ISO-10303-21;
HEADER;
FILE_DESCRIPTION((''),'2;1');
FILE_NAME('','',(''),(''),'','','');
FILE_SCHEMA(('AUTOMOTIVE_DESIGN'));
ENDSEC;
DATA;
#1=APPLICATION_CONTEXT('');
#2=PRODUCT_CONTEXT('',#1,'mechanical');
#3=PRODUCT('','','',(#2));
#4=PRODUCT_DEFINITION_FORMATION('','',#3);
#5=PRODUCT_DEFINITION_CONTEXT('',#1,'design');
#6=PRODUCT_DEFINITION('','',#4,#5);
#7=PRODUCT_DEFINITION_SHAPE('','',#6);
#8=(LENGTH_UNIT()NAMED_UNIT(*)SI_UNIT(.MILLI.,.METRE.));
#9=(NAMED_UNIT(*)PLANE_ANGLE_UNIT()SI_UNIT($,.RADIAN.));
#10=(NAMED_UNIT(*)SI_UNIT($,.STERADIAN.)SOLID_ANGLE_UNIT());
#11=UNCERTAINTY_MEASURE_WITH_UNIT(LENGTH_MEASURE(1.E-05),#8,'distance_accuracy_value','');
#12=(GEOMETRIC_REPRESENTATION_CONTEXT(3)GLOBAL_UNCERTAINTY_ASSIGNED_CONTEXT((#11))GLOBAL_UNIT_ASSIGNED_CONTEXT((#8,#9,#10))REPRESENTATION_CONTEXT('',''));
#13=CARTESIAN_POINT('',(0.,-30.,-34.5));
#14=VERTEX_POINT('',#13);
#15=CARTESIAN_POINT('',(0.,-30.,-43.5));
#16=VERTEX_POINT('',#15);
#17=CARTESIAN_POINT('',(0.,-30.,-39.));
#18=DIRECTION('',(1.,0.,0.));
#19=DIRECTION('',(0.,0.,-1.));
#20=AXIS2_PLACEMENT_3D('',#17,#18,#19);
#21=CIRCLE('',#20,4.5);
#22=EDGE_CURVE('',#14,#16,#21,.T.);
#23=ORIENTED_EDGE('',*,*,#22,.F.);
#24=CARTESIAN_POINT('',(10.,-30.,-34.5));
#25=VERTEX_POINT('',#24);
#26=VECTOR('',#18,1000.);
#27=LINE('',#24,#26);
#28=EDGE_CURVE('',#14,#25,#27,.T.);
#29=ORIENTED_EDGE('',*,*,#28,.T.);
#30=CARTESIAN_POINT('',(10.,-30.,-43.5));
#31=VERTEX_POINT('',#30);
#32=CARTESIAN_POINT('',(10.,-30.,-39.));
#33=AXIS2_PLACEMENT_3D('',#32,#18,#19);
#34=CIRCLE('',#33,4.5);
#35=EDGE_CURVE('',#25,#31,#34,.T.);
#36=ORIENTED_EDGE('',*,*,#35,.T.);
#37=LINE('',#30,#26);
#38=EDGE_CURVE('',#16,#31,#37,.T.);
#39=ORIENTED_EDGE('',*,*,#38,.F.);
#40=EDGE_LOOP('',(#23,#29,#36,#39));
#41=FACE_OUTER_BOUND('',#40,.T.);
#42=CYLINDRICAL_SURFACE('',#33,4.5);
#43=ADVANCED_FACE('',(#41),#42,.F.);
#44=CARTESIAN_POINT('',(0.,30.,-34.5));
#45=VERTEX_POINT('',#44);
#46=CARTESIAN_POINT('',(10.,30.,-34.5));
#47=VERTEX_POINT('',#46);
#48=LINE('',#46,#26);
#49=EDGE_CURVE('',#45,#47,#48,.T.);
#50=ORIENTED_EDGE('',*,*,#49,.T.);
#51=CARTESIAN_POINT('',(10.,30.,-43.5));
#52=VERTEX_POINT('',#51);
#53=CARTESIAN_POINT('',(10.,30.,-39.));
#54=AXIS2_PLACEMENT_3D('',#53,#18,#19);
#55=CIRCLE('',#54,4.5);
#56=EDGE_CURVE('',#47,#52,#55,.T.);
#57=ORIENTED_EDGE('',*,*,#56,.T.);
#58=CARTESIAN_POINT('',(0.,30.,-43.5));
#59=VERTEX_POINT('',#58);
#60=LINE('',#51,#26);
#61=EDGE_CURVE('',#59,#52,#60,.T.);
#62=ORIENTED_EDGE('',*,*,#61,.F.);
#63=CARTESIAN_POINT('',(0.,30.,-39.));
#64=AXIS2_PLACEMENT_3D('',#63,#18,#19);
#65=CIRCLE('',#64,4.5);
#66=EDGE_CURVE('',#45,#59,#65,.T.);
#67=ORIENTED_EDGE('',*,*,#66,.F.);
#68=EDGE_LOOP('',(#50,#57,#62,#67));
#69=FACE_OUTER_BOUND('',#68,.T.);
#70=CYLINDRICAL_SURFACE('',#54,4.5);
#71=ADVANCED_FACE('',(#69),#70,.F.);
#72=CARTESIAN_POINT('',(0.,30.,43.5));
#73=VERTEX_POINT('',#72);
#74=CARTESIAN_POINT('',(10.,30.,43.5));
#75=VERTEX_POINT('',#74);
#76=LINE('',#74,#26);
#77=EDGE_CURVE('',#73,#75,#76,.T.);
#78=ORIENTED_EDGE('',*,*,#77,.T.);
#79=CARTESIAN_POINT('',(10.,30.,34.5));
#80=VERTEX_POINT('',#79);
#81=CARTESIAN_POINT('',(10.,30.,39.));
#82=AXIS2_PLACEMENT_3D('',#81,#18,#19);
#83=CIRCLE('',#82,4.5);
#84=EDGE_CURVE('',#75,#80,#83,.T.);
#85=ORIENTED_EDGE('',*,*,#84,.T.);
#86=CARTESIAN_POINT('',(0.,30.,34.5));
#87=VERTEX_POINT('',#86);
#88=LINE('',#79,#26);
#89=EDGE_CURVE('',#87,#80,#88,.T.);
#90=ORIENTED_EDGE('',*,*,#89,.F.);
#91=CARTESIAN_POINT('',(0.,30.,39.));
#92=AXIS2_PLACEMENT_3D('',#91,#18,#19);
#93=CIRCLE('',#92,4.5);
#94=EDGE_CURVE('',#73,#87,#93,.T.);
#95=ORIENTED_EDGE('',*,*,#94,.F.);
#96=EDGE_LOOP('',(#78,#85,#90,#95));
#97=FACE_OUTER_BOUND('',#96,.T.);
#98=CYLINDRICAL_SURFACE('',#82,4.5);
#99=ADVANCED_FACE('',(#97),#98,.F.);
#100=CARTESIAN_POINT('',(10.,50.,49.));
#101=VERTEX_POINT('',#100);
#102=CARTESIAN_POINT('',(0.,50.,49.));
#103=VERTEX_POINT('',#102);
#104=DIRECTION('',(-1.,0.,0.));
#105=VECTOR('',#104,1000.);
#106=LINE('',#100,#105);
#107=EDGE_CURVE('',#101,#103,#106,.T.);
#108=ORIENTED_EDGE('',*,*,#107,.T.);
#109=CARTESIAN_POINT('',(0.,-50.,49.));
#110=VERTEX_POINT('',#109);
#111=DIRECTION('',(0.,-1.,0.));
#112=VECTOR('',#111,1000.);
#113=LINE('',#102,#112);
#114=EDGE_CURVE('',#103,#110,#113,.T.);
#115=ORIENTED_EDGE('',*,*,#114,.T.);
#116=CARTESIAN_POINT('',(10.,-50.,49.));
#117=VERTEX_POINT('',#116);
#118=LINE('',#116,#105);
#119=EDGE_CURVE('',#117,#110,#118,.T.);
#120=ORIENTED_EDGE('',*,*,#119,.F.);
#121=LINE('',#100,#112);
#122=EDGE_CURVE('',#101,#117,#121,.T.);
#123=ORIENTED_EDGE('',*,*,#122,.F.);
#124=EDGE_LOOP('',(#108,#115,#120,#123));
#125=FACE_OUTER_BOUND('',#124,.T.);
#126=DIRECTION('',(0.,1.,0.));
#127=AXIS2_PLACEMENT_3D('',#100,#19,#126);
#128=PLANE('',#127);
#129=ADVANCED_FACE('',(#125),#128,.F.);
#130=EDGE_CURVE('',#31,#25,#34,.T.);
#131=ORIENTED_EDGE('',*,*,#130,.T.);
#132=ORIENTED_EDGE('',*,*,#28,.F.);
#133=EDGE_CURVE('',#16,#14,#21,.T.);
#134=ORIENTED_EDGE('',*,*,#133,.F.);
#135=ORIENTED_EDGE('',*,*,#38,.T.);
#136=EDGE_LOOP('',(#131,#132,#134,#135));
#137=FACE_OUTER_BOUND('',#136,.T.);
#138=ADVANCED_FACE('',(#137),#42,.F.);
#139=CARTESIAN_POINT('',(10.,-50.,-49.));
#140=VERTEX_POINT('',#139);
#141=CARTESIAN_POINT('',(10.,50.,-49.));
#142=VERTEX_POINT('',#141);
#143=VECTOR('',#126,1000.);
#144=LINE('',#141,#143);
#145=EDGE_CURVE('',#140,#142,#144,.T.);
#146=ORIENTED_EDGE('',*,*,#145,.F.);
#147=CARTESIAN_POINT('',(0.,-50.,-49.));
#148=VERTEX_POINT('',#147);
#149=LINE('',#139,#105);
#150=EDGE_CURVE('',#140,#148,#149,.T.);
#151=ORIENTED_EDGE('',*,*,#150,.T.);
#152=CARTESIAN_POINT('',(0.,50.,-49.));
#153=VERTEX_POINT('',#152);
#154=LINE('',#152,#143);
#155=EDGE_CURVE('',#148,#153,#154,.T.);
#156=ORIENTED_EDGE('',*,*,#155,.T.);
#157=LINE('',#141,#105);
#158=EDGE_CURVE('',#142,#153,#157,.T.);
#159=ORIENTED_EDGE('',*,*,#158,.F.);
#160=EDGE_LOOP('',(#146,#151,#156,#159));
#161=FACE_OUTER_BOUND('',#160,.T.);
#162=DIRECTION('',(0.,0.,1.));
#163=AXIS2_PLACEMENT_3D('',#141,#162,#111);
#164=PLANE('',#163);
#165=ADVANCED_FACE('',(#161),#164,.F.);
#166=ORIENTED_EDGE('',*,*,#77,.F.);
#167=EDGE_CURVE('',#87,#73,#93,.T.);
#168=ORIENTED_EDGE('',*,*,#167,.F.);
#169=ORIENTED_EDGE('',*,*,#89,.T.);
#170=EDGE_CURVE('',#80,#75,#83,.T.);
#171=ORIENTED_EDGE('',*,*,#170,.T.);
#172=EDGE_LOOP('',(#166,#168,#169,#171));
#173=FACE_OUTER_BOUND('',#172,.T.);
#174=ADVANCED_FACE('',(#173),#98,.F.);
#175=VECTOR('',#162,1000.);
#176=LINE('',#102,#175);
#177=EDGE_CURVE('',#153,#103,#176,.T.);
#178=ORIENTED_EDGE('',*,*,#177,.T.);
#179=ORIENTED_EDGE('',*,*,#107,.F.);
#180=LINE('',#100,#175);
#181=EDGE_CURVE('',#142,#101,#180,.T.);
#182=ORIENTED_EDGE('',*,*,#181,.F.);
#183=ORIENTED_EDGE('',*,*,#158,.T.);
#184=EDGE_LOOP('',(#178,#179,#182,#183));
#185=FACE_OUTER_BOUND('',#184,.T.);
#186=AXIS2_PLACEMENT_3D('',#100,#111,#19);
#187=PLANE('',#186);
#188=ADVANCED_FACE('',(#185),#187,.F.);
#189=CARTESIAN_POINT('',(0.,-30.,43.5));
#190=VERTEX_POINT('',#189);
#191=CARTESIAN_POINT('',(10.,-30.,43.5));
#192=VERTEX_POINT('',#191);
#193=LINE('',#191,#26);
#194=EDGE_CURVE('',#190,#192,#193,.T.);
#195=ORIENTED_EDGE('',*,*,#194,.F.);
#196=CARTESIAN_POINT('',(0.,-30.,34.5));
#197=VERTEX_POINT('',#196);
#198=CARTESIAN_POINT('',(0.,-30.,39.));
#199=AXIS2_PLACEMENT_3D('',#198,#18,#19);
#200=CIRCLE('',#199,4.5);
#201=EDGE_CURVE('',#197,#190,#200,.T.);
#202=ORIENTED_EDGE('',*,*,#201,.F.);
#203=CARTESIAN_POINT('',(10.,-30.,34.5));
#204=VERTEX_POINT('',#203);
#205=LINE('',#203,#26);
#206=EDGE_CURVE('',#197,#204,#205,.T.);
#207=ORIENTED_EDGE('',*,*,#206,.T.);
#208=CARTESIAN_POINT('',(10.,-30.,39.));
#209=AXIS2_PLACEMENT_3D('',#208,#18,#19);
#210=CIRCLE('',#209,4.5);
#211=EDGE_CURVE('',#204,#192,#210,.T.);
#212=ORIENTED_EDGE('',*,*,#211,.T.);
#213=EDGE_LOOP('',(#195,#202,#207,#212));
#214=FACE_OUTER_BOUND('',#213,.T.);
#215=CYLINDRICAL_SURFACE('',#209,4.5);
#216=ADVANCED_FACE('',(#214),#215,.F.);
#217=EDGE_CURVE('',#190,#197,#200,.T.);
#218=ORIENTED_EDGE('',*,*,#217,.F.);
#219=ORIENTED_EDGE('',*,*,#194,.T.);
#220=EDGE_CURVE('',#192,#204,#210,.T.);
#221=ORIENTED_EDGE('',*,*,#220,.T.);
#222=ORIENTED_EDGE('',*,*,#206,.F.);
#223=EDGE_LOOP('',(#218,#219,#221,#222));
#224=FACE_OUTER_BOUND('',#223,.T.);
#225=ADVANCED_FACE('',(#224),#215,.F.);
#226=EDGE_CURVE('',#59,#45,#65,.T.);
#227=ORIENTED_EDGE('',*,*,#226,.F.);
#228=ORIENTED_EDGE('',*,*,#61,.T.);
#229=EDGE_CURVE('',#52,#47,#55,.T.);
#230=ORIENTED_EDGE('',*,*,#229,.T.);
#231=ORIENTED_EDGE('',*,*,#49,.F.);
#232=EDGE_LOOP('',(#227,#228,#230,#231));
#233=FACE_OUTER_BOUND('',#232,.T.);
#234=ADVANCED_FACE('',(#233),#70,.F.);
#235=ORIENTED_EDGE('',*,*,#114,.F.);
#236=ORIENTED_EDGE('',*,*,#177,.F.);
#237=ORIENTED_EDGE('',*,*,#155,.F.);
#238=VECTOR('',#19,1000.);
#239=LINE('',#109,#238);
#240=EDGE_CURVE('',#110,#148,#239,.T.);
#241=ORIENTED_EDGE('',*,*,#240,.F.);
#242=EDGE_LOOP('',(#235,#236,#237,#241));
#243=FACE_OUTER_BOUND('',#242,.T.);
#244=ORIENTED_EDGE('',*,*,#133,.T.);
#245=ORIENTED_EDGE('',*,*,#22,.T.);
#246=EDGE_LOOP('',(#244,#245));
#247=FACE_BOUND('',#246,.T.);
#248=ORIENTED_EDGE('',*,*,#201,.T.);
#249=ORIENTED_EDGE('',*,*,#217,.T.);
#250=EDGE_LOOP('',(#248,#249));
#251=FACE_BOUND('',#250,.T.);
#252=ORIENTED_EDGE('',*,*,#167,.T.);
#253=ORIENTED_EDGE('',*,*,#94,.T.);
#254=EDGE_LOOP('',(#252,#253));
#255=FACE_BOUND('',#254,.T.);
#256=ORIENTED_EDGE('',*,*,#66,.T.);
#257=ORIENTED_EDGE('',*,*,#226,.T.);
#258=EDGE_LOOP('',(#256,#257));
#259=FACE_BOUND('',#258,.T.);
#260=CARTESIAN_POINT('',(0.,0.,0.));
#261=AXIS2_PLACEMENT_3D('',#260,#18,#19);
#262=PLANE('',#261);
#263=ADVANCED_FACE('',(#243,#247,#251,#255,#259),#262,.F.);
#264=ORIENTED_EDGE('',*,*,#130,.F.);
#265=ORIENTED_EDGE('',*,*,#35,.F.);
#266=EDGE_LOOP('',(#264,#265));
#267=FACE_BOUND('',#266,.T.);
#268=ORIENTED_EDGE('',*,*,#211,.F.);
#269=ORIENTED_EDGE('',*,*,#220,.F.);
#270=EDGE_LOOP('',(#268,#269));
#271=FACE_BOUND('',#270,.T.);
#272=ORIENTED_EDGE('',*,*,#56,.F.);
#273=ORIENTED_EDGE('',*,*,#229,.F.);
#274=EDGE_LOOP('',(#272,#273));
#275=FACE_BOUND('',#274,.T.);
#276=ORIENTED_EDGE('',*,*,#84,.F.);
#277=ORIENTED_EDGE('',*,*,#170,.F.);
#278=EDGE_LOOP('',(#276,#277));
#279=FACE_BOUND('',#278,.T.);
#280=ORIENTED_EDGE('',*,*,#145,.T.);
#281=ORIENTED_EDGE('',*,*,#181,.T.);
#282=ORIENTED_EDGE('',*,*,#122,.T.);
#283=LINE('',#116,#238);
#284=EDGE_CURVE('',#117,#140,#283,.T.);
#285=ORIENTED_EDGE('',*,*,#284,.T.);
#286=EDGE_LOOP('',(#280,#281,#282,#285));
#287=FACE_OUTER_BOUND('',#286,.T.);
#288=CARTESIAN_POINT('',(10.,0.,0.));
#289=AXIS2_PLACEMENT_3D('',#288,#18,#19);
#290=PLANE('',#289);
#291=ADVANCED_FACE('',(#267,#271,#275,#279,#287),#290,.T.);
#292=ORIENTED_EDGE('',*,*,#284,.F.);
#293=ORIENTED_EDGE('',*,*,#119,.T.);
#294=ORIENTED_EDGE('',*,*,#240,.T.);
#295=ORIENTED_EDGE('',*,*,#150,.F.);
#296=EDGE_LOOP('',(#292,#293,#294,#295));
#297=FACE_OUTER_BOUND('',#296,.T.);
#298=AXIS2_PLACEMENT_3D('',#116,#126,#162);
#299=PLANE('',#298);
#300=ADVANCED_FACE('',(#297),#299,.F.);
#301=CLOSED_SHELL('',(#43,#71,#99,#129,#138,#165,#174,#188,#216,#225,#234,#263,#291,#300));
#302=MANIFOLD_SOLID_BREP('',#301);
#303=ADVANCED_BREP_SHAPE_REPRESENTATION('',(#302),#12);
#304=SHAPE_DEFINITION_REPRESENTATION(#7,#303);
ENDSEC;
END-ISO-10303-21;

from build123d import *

# Parameters (mm, degrees)
SKETCH_1_W            = 98
SKETCH_1_H            = 100
EXTRUDE_1_DEPTH       = 10
HOLE_WIZARD_9_0_9_1_D = 9


with BuildPart() as part:
    # 草图1 → 凸台-拉伸1 (new body)
    with BuildSketch(Plane(origin=(0, 0, 0), x_dir=(0, 0, -1), z_dir=(1, 0, 0))):
        Rectangle(SKETCH_1_W, SKETCH_1_H)
    extrude(amount=EXTRUDE_1_DEPTH)

    # Ø9.0 (9) 直径孔1 (through all)
    with Locations(Plane(origin=(10, 0, 0), x_dir=(0, 0, -1), z_dir=(1, 0, 0))):
        with Locations((-39, 30), (39, 30), (-39, -30), (39, -30)):
            Hole(HOLE_WIZARD_9_0_9_1_D / 2)


solid = part.part
